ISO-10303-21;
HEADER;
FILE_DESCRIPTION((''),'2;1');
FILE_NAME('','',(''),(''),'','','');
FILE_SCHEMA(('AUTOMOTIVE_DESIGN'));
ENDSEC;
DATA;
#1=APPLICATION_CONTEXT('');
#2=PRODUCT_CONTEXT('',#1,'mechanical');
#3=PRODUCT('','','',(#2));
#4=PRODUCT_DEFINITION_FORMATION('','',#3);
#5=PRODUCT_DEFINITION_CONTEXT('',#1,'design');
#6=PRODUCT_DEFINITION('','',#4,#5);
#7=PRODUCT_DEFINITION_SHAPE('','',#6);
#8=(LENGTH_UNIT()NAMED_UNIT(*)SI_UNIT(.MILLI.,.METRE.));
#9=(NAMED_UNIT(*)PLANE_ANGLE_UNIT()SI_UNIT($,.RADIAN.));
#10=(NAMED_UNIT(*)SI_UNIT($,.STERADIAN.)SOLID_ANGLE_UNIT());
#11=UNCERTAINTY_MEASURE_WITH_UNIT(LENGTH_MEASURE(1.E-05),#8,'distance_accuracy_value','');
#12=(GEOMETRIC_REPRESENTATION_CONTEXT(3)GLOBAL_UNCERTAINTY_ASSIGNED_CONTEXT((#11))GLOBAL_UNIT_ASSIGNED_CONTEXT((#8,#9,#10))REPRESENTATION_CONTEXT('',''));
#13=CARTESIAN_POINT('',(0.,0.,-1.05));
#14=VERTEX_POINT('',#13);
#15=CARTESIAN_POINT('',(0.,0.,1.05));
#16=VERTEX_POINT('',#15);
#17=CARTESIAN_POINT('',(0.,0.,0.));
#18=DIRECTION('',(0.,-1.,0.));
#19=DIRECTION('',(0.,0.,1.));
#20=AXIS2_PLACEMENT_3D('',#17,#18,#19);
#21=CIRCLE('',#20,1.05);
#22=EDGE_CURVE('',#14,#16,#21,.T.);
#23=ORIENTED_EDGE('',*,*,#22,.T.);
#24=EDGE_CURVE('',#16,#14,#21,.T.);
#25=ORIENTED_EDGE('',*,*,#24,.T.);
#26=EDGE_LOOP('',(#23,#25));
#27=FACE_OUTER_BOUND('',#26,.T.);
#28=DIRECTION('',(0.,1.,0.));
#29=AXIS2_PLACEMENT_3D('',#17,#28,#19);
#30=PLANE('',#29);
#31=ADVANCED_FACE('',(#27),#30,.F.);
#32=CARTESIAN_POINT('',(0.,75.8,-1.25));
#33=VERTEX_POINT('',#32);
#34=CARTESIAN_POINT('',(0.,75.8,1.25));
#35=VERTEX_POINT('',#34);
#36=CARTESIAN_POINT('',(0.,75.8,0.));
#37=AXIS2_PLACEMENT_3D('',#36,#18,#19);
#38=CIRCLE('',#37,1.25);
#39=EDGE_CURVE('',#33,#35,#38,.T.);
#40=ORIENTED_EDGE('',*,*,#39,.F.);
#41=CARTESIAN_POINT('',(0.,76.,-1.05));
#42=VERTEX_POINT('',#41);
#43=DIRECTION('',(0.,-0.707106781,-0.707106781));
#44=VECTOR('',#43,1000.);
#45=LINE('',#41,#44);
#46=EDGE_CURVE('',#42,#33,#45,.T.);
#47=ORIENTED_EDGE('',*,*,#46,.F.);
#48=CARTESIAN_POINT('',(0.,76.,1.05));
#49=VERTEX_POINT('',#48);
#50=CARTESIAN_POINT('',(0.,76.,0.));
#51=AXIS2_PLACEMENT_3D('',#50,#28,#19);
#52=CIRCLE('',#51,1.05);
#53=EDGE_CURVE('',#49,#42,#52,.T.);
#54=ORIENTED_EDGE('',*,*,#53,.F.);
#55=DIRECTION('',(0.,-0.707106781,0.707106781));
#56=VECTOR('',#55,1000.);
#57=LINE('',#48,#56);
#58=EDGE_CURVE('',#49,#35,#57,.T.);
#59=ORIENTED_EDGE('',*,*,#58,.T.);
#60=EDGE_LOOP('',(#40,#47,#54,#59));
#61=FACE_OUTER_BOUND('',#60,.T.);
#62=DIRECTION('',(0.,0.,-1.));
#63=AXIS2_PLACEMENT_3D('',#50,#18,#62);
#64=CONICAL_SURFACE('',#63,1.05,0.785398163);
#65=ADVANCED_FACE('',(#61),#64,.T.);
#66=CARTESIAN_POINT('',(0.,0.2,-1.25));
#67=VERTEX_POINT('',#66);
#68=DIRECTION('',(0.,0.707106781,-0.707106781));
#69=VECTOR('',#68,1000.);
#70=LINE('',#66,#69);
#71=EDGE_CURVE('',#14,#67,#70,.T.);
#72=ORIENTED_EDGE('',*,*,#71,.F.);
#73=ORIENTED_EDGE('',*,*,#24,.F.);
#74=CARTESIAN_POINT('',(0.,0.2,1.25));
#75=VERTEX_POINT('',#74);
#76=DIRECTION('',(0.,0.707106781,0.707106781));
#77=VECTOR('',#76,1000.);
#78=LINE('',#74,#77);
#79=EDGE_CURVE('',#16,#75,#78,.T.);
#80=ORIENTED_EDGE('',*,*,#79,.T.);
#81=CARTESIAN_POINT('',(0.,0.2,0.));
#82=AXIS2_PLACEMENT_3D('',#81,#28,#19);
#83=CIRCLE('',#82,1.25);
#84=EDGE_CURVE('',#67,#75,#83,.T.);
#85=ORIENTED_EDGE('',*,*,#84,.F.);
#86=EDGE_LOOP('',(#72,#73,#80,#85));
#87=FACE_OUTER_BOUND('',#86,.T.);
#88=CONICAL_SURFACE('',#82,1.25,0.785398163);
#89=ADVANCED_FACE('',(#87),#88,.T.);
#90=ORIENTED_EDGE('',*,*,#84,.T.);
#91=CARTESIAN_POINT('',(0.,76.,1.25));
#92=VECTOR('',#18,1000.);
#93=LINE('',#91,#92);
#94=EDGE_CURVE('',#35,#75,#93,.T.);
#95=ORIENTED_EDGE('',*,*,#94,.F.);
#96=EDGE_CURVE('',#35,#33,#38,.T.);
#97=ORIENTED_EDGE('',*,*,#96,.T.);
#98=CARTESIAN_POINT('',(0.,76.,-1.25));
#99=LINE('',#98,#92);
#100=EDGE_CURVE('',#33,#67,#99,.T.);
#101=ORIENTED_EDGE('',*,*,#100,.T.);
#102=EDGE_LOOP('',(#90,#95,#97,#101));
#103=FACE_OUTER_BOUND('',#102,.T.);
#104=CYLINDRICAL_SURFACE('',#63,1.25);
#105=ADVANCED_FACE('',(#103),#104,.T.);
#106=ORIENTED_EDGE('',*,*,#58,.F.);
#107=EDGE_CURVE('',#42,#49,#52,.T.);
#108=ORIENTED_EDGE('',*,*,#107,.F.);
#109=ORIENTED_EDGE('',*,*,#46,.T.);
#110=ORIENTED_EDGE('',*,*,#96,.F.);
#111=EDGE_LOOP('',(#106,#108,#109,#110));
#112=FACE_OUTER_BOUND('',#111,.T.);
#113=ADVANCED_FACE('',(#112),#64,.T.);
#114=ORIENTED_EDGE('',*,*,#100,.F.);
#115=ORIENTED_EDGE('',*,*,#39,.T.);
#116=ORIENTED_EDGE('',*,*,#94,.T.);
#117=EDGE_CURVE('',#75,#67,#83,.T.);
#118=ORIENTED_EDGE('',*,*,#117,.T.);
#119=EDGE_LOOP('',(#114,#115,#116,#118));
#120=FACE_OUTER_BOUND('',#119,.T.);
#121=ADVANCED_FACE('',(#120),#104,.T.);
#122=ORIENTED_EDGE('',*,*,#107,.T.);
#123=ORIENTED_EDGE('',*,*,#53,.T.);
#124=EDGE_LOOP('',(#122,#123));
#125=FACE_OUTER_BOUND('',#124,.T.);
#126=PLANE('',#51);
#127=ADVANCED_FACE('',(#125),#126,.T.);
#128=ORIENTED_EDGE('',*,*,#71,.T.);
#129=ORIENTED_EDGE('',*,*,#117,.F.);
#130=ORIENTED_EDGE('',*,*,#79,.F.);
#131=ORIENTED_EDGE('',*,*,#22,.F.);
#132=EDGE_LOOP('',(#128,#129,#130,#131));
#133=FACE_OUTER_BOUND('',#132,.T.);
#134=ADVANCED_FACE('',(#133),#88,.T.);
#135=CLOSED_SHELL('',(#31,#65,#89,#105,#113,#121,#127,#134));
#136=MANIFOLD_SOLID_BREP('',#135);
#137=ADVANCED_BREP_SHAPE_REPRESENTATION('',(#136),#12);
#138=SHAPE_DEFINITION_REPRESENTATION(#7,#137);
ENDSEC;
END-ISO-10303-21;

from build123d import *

# Parameters (mm, degrees)
SKETCH_1_R      = 1.25
EXTRUDE_1_DEPTH = 76
CHAMFER_1_SIZE  = 0.2


with BuildPart() as part:
    # 草图1 → 凸台-拉伸1 (new body)
    with BuildSketch(Plane(origin=(0, 0, 0), x_dir=(1, 0, 0), z_dir=(0, 1, 0))):
        with Locations(Location((0, 0, 0), (0, 0, 270))):
            Circle(SKETCH_1_R)
    extrude(amount=EXTRUDE_1_DEPTH)

    # 倒角1
    chamfer_1_edges = [part.edges().sort_by_distance(p)[0] for p in [
        (0, 0, -1.25),
        (0, 76, -1.25),
    ]]
    chamfer(chamfer_1_edges, length=CHAMFER_1_SIZE)


solid = part.part
